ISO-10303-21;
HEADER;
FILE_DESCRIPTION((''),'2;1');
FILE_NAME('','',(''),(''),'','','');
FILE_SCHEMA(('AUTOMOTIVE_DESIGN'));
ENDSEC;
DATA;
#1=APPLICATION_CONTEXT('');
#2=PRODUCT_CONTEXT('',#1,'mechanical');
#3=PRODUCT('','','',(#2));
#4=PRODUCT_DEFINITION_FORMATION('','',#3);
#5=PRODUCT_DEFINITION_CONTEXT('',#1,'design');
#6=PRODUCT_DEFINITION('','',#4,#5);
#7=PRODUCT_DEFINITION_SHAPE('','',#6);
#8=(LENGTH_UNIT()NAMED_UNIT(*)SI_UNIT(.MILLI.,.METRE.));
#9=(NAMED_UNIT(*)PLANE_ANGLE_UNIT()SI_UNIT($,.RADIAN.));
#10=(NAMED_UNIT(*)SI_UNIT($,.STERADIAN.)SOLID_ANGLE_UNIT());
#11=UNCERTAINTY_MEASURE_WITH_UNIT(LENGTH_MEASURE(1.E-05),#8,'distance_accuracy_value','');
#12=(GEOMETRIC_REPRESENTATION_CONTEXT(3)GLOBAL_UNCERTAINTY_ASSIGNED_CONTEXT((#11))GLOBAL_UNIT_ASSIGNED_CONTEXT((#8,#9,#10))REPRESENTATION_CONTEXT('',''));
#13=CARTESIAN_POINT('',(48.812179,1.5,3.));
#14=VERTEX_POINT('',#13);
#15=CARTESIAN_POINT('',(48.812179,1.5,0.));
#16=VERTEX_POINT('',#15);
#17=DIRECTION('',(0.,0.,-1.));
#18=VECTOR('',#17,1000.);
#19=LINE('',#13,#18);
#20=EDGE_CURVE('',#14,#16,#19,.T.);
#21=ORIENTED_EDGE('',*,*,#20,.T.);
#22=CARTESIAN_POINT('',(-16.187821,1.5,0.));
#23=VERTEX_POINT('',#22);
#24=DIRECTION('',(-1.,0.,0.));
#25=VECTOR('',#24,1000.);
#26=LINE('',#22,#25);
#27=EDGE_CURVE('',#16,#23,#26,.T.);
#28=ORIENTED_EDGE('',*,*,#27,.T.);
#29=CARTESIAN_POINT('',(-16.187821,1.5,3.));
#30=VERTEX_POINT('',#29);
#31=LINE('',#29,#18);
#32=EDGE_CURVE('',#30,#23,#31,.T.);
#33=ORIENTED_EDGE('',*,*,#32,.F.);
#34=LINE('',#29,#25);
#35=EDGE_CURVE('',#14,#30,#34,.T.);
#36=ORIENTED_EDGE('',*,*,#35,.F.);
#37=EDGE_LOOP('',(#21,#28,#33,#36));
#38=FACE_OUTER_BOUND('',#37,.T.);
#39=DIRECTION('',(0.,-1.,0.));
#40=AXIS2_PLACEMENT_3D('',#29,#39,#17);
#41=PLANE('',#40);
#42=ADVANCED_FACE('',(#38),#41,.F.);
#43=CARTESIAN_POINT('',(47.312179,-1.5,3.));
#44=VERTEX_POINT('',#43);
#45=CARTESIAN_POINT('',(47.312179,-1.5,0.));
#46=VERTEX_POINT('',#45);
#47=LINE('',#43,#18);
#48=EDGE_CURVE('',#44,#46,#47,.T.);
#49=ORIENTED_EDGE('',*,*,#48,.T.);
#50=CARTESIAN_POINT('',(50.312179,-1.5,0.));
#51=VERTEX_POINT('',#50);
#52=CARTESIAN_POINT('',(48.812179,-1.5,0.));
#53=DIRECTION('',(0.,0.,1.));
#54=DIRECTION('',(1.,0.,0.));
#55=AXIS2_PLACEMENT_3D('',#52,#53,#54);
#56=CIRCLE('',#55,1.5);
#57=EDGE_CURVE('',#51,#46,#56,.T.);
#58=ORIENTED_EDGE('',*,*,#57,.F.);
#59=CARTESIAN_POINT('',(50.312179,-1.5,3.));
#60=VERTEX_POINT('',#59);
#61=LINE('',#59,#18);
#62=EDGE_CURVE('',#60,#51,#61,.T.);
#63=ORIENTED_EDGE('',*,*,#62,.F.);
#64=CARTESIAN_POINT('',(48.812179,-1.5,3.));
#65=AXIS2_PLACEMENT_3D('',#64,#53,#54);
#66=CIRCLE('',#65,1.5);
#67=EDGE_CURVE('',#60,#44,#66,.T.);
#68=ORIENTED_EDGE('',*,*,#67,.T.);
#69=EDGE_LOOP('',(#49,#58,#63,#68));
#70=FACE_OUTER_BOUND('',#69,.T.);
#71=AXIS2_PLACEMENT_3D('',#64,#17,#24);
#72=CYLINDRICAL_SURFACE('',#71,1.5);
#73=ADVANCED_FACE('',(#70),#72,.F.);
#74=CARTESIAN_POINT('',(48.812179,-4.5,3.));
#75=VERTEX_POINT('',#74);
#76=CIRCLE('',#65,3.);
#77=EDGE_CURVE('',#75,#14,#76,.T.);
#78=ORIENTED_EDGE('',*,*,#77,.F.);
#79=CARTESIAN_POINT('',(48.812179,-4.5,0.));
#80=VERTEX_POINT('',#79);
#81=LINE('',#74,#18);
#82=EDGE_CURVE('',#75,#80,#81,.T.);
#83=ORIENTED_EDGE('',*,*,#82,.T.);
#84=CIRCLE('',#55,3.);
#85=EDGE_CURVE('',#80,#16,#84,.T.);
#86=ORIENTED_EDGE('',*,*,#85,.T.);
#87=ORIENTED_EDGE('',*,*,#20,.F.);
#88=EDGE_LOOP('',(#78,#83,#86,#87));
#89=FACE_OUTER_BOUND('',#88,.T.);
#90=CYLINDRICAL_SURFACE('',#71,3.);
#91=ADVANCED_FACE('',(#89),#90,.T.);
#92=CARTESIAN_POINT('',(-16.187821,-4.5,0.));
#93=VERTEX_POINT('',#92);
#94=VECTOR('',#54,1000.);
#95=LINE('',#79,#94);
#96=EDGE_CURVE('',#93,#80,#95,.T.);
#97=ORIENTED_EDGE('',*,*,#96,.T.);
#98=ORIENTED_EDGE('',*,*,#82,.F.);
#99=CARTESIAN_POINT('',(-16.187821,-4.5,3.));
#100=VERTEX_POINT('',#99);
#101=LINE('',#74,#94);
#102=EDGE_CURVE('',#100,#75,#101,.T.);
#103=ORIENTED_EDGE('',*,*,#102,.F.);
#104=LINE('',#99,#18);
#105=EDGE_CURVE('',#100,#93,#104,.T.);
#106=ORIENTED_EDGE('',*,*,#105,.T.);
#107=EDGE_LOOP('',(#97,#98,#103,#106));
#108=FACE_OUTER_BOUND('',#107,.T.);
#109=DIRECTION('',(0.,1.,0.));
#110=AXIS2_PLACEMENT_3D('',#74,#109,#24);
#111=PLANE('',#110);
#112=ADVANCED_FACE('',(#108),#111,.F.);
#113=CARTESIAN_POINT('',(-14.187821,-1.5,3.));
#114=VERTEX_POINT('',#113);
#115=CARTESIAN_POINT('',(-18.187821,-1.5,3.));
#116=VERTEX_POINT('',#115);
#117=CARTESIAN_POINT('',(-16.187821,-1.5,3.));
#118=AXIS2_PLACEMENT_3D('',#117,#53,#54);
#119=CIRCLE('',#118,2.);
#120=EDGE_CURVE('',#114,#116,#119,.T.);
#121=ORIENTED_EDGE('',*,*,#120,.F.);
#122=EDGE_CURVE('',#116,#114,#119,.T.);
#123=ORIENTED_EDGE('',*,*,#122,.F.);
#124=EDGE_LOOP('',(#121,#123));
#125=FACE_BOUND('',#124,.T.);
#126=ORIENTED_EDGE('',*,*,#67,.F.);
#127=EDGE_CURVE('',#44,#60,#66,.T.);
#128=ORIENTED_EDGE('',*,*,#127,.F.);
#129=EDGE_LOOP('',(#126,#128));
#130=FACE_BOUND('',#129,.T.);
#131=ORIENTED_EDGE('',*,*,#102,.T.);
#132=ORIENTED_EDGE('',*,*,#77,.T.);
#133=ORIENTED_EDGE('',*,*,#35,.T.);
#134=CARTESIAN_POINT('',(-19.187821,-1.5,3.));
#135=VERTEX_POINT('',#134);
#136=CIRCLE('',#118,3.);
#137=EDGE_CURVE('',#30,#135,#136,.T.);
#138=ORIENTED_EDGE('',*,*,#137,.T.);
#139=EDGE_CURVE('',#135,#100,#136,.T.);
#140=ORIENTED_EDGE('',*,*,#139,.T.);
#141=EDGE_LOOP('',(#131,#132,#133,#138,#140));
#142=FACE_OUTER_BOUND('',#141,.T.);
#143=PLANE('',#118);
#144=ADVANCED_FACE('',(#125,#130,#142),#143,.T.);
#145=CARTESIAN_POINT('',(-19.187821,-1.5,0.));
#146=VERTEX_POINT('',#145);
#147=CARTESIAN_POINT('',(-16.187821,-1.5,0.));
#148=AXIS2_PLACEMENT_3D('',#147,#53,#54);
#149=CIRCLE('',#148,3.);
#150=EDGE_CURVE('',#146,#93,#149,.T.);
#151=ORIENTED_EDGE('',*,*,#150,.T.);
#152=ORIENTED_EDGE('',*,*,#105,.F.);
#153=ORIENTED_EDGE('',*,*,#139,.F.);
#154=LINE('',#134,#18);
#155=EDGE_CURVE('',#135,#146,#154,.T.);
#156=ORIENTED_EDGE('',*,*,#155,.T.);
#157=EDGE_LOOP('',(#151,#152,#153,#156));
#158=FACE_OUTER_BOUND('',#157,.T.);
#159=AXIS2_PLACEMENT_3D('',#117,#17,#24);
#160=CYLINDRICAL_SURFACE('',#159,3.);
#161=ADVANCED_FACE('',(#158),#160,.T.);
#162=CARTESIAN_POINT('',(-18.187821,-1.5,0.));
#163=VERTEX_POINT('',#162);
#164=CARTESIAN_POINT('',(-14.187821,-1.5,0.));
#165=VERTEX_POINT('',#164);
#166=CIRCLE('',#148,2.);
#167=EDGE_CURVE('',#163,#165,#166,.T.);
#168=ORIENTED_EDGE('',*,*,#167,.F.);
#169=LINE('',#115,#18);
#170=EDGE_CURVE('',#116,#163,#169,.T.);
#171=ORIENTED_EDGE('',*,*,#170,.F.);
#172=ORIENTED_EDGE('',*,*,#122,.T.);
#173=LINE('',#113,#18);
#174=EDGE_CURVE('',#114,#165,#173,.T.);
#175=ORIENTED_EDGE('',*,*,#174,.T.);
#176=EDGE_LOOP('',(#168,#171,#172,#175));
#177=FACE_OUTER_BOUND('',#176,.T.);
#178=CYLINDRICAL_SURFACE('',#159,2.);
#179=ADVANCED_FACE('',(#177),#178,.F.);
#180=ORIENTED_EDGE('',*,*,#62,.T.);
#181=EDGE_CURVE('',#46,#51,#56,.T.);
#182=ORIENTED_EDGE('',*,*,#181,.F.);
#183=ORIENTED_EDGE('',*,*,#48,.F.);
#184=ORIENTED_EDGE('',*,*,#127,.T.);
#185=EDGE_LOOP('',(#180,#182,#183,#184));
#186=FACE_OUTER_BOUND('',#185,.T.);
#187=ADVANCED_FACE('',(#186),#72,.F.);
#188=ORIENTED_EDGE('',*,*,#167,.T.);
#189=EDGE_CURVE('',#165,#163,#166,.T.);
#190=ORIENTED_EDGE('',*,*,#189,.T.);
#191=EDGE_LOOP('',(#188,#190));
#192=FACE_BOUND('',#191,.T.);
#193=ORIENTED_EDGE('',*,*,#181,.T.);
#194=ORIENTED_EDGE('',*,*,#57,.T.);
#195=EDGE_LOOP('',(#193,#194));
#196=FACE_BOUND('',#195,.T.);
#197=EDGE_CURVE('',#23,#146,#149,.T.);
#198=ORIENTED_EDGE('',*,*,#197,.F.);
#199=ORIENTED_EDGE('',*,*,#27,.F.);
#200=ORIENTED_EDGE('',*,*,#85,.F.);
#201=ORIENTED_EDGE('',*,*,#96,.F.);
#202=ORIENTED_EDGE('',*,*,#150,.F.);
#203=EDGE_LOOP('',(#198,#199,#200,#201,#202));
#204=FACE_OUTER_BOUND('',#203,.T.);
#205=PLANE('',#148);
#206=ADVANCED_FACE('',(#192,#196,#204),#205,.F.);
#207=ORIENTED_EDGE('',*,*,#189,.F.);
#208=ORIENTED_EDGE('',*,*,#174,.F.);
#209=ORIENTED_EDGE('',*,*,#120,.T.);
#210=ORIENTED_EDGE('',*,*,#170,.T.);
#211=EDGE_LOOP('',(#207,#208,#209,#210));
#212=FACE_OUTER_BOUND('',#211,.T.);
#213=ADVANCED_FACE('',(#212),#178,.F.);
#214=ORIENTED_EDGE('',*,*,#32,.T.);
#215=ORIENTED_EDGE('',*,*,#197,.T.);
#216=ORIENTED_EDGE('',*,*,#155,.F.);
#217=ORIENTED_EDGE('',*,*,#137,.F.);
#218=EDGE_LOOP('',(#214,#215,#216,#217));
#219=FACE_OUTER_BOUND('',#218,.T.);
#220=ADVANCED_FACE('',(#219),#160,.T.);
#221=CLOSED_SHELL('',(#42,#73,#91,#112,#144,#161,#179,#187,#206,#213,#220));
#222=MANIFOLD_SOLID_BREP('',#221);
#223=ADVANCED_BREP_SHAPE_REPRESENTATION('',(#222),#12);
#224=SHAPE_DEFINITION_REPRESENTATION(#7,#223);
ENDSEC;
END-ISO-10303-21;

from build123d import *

# Parameters (mm, degrees)
SKETCH1_R           = 4
SKETCH1_R_2         = 3
BOSS_EXTRUDE1_DEPTH = 6
SCALE1_SCALE        = 0.5


with BuildPart() as part:
    # Sketch1 → Boss-Extrude1 (new body)
    with BuildSketch(Plane.XY):
        with BuildLine():
            Line((-32.375641401, 3), (97.624358599, 3))
            ThreePointArc((97.624358599, 3), (103.624358599, -3), (97.624358599, -9))
            Line((97.624358599, -9), (-32.375641401, -9))
            ThreePointArc((-32.375641401, -9), (-38.375641401, -3), (-32.375641401, 3))
        make_face()
        with Locations((-32.375641401, -3)):
            Circle(SKETCH1_R, mode=Mode.SUBTRACT)
        with Locations((97.624358599, -3)):
            Circle(SKETCH1_R_2, mode=Mode.SUBTRACT)
    extrude(amount=BOSS_EXTRUDE1_DEPTH)


with BuildPart() as part_1:
    # Scale1: scaled about (0, 0, 0)
    add(part.part.scale(SCALE1_SCALE))


solid = part_1.part
